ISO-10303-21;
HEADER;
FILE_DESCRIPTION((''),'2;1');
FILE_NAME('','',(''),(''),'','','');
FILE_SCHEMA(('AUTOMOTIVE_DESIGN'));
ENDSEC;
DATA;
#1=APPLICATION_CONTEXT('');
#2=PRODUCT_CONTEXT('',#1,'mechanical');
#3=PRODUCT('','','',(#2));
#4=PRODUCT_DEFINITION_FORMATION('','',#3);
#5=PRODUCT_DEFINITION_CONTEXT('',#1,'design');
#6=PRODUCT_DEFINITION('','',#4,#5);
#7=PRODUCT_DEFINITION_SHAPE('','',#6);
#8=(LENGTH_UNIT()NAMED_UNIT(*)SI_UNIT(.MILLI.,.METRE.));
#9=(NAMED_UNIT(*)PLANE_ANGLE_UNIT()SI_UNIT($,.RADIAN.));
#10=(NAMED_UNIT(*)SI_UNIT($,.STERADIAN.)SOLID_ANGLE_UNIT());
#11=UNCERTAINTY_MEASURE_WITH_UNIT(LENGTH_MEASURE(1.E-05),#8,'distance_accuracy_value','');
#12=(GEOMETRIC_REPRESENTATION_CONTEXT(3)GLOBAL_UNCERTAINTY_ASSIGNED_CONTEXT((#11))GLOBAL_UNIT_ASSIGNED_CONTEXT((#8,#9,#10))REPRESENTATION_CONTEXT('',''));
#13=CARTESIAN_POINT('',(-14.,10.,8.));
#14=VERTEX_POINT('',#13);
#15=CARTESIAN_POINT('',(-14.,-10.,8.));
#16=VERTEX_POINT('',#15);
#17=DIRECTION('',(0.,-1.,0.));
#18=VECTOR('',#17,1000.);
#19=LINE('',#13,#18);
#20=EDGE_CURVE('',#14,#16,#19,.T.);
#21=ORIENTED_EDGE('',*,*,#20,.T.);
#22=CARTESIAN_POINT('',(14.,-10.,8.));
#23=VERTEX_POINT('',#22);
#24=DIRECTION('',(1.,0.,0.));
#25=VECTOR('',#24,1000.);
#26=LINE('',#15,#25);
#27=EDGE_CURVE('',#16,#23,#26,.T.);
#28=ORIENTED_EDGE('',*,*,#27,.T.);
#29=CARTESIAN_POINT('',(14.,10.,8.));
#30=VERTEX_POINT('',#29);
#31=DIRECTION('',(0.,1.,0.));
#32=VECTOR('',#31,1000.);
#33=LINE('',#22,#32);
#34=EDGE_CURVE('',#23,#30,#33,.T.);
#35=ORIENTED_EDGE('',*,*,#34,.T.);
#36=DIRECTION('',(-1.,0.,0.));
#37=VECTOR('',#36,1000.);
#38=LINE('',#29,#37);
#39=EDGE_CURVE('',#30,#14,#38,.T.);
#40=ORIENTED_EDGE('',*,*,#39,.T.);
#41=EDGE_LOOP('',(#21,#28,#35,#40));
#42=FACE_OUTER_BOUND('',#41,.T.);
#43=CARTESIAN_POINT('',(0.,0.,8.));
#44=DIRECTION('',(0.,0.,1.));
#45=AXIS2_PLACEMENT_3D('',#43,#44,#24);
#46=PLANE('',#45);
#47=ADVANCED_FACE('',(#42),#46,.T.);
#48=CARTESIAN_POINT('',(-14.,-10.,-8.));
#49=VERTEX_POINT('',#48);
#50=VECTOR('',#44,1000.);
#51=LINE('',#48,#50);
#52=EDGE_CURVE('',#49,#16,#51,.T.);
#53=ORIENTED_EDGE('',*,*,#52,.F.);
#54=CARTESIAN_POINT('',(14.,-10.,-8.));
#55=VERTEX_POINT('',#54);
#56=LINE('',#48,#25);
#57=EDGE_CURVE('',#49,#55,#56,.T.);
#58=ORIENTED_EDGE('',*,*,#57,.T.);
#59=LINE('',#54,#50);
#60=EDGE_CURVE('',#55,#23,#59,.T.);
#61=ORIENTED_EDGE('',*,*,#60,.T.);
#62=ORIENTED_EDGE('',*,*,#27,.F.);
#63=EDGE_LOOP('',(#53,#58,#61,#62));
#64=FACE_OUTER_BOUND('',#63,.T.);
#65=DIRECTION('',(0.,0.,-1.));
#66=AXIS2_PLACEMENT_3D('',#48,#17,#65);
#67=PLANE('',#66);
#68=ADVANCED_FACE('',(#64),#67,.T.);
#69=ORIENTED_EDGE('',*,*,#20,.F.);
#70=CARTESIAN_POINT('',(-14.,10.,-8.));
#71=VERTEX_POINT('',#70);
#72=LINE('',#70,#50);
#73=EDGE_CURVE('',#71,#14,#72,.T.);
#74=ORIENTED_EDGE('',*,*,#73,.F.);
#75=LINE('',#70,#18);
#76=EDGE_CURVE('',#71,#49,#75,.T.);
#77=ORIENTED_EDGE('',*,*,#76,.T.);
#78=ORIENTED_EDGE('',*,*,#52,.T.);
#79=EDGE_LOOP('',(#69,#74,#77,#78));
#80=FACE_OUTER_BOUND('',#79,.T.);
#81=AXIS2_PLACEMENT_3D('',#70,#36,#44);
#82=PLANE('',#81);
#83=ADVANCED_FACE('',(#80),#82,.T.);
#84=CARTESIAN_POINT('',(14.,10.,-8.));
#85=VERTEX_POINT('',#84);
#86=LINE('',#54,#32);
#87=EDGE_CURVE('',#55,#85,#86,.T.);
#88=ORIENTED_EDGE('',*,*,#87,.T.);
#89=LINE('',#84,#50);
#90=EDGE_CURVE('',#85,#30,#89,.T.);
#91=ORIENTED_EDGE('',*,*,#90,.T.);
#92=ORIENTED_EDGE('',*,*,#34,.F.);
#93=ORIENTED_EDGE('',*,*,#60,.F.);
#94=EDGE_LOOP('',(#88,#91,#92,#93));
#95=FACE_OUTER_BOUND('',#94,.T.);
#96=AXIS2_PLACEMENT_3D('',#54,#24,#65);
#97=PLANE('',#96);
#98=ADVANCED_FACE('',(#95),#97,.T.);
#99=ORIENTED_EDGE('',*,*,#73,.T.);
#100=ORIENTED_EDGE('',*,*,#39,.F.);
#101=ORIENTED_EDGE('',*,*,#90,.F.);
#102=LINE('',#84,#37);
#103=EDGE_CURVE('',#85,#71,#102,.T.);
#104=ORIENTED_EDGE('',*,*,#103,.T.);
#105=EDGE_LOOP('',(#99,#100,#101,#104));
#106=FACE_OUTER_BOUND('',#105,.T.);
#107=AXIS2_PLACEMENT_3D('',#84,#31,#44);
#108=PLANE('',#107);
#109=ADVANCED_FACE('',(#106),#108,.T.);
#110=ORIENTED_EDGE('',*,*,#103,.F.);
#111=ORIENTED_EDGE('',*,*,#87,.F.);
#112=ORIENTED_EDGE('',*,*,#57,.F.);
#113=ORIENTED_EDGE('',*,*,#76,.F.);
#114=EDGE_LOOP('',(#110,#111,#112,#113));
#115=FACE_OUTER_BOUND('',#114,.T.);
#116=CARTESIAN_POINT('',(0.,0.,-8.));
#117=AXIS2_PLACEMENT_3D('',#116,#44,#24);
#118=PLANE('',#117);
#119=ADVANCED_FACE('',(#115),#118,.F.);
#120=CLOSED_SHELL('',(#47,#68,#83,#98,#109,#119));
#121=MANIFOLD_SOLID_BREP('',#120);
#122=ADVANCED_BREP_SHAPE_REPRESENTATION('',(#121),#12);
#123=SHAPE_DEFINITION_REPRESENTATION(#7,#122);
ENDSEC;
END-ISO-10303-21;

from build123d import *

# Parameters (mm, degrees)
SKETCH_1_W      = 28
SKETCH_1_H      = 20
EXTRUDE_1_DEPTH = 8


with BuildPart() as part:
    # 草图1 → 凸台-拉伸1 (new, symmetric)
    with BuildSketch(Plane.XY):
        Rectangle(SKETCH_1_W, SKETCH_1_H)
    extrude(amount=EXTRUDE_1_DEPTH, both=True)


solid = part.part
